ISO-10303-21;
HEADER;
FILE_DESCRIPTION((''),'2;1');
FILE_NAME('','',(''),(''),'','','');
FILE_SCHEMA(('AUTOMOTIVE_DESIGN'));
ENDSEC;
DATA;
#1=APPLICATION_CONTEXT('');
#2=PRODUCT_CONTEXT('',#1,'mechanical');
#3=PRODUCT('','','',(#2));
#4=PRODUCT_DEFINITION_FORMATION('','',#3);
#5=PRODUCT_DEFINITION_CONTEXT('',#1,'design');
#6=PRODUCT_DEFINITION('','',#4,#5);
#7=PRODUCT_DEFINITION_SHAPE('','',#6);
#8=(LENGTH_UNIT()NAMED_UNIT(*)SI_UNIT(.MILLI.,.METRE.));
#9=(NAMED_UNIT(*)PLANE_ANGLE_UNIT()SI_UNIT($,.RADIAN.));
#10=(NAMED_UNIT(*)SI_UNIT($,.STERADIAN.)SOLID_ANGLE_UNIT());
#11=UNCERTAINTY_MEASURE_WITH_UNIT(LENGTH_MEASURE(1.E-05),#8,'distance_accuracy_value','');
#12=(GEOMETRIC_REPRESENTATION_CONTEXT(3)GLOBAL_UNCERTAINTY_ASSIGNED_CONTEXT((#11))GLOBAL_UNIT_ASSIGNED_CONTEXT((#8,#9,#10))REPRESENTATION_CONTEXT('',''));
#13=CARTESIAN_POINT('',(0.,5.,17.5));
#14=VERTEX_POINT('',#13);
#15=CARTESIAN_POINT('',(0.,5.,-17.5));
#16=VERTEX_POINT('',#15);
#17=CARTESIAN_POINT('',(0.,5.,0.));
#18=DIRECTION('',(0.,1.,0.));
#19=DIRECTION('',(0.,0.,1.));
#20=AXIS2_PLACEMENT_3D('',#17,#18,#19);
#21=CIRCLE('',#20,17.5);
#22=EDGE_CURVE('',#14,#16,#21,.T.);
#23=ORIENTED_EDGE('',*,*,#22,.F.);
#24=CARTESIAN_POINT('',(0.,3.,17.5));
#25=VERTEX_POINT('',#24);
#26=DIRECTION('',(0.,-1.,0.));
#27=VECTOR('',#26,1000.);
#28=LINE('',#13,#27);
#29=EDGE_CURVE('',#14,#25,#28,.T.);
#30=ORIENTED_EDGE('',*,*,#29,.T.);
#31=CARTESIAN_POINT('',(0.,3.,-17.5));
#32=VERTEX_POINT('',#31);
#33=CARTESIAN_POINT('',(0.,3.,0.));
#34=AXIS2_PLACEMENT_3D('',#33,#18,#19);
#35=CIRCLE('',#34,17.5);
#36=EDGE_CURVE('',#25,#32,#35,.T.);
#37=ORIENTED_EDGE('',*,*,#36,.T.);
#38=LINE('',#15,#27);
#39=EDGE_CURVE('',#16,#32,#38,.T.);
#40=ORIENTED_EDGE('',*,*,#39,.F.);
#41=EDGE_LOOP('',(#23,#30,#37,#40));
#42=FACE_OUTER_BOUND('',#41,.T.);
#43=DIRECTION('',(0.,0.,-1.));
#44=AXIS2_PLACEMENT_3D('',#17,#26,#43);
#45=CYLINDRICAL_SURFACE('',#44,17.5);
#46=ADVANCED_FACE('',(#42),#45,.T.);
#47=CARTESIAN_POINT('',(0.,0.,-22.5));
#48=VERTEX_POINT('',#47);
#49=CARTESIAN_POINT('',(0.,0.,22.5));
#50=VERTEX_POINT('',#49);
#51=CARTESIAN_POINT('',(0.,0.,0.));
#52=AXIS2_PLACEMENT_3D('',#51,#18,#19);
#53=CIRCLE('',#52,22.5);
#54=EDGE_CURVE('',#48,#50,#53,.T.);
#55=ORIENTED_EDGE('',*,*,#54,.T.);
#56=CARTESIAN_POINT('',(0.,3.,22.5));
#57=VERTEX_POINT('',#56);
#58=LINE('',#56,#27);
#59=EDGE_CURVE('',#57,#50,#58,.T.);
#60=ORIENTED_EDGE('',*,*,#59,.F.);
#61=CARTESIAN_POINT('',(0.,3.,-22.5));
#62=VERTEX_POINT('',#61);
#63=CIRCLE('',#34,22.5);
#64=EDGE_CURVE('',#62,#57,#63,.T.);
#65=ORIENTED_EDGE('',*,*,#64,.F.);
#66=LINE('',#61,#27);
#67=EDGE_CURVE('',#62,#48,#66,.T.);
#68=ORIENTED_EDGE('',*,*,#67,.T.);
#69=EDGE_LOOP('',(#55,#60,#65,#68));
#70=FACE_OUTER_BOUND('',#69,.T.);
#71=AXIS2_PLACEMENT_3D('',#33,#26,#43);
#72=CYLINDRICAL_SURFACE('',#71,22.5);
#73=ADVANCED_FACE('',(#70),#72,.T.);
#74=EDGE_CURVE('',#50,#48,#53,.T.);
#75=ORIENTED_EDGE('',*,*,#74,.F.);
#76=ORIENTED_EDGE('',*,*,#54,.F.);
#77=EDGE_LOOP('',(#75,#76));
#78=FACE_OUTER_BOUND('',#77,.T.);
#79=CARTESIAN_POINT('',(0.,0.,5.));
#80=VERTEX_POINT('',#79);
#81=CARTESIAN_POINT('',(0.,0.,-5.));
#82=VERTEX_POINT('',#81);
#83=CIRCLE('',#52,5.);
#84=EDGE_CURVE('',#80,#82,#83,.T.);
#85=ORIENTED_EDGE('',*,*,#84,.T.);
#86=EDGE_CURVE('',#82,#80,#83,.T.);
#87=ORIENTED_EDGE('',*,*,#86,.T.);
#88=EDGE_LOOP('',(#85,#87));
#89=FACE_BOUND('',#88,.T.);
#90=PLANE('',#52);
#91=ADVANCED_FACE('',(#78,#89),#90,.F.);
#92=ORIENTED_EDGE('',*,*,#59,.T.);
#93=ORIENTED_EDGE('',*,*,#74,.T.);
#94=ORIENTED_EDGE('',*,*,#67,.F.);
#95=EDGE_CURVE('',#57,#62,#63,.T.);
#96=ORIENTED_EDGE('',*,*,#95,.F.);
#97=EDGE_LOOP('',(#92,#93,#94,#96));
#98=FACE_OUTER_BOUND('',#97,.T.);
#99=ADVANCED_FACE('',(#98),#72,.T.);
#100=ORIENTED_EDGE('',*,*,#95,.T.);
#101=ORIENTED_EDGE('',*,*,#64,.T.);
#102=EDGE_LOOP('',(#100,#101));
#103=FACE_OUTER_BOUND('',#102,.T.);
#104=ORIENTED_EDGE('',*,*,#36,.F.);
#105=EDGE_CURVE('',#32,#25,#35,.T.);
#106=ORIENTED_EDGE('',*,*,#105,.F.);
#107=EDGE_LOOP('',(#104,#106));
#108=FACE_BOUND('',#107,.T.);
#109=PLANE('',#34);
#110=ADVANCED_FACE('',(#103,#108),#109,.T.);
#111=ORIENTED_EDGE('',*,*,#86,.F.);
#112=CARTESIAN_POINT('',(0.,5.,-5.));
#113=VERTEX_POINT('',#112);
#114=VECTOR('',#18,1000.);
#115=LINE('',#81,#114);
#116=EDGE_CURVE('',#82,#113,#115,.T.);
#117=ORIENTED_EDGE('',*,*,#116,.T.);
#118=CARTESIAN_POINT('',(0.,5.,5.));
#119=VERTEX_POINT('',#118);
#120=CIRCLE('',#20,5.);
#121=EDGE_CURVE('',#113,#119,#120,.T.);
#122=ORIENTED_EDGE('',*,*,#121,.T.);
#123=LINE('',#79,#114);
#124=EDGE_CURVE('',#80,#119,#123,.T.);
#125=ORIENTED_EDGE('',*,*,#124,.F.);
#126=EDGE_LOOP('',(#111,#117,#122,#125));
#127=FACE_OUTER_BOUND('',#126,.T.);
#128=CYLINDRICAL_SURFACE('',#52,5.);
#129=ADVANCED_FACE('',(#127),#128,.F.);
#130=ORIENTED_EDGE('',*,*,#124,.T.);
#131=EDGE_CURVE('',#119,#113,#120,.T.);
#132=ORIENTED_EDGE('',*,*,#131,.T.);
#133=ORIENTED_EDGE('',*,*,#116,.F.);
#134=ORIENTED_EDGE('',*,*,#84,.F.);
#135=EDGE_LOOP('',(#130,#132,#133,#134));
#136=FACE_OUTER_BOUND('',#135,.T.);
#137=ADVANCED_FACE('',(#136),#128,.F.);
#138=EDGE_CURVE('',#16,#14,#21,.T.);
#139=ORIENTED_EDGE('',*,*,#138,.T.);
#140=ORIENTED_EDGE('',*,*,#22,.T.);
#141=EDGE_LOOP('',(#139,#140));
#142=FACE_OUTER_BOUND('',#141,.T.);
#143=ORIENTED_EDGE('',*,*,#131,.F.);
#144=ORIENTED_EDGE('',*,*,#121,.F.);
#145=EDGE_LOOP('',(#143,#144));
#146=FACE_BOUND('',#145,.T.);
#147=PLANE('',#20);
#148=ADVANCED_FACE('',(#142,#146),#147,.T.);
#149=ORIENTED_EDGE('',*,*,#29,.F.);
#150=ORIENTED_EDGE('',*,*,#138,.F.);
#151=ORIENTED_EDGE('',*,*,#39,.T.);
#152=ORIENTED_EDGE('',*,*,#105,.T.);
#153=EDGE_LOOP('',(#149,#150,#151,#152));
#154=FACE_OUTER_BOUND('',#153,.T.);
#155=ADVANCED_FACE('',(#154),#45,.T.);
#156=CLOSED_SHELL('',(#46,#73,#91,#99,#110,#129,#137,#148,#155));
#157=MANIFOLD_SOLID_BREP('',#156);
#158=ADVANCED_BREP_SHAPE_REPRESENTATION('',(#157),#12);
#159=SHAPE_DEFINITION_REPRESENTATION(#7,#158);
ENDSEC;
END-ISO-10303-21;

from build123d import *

# Parameters (mm, degrees)
SKETCH_1_R          = 22.5
EXTRUDE_1_DEPTH     = 3
SKETCH_2_R          = 17.5
EXTRUDE_2_DEPTH     = 2
SKETCH_3_R          = 5
CUT_EXTRUDE_1_DEPTH = 33.210246817


with BuildPart() as part:
    # 草图1 → 凸台-拉伸1 (new body)
    with BuildSketch(Plane(origin=(0, 0, 0), x_dir=(1, 0, 0), z_dir=(0, 1, 0))):
        with Locations(Location((0, 0, 0), (0, 0, 270))):
            Circle(SKETCH_1_R)
    extrude(amount=EXTRUDE_1_DEPTH)

    # 草图2 → 凸台-拉伸2 (add)
    with BuildSketch(Plane(origin=(0, 3, 0), x_dir=(1, 0, 0), z_dir=(0, 1, 0))):
        with Locations(Location((0, 0, 0), (0, 0, 270))):
            Circle(SKETCH_2_R)
    extrude(amount=EXTRUDE_2_DEPTH)

    # 草图3 → 切除-拉伸1 (cut, through all)
    with BuildSketch(Plane(origin=(0, 5, 0), x_dir=(1, 0, 0), z_dir=(0, 1, 0))):
        with Locations(Location((0, 0, 0), (0, 0, 270))):
            Circle(SKETCH_3_R)
    extrude(amount=-CUT_EXTRUDE_1_DEPTH, mode=Mode.SUBTRACT)


solid = part.part
